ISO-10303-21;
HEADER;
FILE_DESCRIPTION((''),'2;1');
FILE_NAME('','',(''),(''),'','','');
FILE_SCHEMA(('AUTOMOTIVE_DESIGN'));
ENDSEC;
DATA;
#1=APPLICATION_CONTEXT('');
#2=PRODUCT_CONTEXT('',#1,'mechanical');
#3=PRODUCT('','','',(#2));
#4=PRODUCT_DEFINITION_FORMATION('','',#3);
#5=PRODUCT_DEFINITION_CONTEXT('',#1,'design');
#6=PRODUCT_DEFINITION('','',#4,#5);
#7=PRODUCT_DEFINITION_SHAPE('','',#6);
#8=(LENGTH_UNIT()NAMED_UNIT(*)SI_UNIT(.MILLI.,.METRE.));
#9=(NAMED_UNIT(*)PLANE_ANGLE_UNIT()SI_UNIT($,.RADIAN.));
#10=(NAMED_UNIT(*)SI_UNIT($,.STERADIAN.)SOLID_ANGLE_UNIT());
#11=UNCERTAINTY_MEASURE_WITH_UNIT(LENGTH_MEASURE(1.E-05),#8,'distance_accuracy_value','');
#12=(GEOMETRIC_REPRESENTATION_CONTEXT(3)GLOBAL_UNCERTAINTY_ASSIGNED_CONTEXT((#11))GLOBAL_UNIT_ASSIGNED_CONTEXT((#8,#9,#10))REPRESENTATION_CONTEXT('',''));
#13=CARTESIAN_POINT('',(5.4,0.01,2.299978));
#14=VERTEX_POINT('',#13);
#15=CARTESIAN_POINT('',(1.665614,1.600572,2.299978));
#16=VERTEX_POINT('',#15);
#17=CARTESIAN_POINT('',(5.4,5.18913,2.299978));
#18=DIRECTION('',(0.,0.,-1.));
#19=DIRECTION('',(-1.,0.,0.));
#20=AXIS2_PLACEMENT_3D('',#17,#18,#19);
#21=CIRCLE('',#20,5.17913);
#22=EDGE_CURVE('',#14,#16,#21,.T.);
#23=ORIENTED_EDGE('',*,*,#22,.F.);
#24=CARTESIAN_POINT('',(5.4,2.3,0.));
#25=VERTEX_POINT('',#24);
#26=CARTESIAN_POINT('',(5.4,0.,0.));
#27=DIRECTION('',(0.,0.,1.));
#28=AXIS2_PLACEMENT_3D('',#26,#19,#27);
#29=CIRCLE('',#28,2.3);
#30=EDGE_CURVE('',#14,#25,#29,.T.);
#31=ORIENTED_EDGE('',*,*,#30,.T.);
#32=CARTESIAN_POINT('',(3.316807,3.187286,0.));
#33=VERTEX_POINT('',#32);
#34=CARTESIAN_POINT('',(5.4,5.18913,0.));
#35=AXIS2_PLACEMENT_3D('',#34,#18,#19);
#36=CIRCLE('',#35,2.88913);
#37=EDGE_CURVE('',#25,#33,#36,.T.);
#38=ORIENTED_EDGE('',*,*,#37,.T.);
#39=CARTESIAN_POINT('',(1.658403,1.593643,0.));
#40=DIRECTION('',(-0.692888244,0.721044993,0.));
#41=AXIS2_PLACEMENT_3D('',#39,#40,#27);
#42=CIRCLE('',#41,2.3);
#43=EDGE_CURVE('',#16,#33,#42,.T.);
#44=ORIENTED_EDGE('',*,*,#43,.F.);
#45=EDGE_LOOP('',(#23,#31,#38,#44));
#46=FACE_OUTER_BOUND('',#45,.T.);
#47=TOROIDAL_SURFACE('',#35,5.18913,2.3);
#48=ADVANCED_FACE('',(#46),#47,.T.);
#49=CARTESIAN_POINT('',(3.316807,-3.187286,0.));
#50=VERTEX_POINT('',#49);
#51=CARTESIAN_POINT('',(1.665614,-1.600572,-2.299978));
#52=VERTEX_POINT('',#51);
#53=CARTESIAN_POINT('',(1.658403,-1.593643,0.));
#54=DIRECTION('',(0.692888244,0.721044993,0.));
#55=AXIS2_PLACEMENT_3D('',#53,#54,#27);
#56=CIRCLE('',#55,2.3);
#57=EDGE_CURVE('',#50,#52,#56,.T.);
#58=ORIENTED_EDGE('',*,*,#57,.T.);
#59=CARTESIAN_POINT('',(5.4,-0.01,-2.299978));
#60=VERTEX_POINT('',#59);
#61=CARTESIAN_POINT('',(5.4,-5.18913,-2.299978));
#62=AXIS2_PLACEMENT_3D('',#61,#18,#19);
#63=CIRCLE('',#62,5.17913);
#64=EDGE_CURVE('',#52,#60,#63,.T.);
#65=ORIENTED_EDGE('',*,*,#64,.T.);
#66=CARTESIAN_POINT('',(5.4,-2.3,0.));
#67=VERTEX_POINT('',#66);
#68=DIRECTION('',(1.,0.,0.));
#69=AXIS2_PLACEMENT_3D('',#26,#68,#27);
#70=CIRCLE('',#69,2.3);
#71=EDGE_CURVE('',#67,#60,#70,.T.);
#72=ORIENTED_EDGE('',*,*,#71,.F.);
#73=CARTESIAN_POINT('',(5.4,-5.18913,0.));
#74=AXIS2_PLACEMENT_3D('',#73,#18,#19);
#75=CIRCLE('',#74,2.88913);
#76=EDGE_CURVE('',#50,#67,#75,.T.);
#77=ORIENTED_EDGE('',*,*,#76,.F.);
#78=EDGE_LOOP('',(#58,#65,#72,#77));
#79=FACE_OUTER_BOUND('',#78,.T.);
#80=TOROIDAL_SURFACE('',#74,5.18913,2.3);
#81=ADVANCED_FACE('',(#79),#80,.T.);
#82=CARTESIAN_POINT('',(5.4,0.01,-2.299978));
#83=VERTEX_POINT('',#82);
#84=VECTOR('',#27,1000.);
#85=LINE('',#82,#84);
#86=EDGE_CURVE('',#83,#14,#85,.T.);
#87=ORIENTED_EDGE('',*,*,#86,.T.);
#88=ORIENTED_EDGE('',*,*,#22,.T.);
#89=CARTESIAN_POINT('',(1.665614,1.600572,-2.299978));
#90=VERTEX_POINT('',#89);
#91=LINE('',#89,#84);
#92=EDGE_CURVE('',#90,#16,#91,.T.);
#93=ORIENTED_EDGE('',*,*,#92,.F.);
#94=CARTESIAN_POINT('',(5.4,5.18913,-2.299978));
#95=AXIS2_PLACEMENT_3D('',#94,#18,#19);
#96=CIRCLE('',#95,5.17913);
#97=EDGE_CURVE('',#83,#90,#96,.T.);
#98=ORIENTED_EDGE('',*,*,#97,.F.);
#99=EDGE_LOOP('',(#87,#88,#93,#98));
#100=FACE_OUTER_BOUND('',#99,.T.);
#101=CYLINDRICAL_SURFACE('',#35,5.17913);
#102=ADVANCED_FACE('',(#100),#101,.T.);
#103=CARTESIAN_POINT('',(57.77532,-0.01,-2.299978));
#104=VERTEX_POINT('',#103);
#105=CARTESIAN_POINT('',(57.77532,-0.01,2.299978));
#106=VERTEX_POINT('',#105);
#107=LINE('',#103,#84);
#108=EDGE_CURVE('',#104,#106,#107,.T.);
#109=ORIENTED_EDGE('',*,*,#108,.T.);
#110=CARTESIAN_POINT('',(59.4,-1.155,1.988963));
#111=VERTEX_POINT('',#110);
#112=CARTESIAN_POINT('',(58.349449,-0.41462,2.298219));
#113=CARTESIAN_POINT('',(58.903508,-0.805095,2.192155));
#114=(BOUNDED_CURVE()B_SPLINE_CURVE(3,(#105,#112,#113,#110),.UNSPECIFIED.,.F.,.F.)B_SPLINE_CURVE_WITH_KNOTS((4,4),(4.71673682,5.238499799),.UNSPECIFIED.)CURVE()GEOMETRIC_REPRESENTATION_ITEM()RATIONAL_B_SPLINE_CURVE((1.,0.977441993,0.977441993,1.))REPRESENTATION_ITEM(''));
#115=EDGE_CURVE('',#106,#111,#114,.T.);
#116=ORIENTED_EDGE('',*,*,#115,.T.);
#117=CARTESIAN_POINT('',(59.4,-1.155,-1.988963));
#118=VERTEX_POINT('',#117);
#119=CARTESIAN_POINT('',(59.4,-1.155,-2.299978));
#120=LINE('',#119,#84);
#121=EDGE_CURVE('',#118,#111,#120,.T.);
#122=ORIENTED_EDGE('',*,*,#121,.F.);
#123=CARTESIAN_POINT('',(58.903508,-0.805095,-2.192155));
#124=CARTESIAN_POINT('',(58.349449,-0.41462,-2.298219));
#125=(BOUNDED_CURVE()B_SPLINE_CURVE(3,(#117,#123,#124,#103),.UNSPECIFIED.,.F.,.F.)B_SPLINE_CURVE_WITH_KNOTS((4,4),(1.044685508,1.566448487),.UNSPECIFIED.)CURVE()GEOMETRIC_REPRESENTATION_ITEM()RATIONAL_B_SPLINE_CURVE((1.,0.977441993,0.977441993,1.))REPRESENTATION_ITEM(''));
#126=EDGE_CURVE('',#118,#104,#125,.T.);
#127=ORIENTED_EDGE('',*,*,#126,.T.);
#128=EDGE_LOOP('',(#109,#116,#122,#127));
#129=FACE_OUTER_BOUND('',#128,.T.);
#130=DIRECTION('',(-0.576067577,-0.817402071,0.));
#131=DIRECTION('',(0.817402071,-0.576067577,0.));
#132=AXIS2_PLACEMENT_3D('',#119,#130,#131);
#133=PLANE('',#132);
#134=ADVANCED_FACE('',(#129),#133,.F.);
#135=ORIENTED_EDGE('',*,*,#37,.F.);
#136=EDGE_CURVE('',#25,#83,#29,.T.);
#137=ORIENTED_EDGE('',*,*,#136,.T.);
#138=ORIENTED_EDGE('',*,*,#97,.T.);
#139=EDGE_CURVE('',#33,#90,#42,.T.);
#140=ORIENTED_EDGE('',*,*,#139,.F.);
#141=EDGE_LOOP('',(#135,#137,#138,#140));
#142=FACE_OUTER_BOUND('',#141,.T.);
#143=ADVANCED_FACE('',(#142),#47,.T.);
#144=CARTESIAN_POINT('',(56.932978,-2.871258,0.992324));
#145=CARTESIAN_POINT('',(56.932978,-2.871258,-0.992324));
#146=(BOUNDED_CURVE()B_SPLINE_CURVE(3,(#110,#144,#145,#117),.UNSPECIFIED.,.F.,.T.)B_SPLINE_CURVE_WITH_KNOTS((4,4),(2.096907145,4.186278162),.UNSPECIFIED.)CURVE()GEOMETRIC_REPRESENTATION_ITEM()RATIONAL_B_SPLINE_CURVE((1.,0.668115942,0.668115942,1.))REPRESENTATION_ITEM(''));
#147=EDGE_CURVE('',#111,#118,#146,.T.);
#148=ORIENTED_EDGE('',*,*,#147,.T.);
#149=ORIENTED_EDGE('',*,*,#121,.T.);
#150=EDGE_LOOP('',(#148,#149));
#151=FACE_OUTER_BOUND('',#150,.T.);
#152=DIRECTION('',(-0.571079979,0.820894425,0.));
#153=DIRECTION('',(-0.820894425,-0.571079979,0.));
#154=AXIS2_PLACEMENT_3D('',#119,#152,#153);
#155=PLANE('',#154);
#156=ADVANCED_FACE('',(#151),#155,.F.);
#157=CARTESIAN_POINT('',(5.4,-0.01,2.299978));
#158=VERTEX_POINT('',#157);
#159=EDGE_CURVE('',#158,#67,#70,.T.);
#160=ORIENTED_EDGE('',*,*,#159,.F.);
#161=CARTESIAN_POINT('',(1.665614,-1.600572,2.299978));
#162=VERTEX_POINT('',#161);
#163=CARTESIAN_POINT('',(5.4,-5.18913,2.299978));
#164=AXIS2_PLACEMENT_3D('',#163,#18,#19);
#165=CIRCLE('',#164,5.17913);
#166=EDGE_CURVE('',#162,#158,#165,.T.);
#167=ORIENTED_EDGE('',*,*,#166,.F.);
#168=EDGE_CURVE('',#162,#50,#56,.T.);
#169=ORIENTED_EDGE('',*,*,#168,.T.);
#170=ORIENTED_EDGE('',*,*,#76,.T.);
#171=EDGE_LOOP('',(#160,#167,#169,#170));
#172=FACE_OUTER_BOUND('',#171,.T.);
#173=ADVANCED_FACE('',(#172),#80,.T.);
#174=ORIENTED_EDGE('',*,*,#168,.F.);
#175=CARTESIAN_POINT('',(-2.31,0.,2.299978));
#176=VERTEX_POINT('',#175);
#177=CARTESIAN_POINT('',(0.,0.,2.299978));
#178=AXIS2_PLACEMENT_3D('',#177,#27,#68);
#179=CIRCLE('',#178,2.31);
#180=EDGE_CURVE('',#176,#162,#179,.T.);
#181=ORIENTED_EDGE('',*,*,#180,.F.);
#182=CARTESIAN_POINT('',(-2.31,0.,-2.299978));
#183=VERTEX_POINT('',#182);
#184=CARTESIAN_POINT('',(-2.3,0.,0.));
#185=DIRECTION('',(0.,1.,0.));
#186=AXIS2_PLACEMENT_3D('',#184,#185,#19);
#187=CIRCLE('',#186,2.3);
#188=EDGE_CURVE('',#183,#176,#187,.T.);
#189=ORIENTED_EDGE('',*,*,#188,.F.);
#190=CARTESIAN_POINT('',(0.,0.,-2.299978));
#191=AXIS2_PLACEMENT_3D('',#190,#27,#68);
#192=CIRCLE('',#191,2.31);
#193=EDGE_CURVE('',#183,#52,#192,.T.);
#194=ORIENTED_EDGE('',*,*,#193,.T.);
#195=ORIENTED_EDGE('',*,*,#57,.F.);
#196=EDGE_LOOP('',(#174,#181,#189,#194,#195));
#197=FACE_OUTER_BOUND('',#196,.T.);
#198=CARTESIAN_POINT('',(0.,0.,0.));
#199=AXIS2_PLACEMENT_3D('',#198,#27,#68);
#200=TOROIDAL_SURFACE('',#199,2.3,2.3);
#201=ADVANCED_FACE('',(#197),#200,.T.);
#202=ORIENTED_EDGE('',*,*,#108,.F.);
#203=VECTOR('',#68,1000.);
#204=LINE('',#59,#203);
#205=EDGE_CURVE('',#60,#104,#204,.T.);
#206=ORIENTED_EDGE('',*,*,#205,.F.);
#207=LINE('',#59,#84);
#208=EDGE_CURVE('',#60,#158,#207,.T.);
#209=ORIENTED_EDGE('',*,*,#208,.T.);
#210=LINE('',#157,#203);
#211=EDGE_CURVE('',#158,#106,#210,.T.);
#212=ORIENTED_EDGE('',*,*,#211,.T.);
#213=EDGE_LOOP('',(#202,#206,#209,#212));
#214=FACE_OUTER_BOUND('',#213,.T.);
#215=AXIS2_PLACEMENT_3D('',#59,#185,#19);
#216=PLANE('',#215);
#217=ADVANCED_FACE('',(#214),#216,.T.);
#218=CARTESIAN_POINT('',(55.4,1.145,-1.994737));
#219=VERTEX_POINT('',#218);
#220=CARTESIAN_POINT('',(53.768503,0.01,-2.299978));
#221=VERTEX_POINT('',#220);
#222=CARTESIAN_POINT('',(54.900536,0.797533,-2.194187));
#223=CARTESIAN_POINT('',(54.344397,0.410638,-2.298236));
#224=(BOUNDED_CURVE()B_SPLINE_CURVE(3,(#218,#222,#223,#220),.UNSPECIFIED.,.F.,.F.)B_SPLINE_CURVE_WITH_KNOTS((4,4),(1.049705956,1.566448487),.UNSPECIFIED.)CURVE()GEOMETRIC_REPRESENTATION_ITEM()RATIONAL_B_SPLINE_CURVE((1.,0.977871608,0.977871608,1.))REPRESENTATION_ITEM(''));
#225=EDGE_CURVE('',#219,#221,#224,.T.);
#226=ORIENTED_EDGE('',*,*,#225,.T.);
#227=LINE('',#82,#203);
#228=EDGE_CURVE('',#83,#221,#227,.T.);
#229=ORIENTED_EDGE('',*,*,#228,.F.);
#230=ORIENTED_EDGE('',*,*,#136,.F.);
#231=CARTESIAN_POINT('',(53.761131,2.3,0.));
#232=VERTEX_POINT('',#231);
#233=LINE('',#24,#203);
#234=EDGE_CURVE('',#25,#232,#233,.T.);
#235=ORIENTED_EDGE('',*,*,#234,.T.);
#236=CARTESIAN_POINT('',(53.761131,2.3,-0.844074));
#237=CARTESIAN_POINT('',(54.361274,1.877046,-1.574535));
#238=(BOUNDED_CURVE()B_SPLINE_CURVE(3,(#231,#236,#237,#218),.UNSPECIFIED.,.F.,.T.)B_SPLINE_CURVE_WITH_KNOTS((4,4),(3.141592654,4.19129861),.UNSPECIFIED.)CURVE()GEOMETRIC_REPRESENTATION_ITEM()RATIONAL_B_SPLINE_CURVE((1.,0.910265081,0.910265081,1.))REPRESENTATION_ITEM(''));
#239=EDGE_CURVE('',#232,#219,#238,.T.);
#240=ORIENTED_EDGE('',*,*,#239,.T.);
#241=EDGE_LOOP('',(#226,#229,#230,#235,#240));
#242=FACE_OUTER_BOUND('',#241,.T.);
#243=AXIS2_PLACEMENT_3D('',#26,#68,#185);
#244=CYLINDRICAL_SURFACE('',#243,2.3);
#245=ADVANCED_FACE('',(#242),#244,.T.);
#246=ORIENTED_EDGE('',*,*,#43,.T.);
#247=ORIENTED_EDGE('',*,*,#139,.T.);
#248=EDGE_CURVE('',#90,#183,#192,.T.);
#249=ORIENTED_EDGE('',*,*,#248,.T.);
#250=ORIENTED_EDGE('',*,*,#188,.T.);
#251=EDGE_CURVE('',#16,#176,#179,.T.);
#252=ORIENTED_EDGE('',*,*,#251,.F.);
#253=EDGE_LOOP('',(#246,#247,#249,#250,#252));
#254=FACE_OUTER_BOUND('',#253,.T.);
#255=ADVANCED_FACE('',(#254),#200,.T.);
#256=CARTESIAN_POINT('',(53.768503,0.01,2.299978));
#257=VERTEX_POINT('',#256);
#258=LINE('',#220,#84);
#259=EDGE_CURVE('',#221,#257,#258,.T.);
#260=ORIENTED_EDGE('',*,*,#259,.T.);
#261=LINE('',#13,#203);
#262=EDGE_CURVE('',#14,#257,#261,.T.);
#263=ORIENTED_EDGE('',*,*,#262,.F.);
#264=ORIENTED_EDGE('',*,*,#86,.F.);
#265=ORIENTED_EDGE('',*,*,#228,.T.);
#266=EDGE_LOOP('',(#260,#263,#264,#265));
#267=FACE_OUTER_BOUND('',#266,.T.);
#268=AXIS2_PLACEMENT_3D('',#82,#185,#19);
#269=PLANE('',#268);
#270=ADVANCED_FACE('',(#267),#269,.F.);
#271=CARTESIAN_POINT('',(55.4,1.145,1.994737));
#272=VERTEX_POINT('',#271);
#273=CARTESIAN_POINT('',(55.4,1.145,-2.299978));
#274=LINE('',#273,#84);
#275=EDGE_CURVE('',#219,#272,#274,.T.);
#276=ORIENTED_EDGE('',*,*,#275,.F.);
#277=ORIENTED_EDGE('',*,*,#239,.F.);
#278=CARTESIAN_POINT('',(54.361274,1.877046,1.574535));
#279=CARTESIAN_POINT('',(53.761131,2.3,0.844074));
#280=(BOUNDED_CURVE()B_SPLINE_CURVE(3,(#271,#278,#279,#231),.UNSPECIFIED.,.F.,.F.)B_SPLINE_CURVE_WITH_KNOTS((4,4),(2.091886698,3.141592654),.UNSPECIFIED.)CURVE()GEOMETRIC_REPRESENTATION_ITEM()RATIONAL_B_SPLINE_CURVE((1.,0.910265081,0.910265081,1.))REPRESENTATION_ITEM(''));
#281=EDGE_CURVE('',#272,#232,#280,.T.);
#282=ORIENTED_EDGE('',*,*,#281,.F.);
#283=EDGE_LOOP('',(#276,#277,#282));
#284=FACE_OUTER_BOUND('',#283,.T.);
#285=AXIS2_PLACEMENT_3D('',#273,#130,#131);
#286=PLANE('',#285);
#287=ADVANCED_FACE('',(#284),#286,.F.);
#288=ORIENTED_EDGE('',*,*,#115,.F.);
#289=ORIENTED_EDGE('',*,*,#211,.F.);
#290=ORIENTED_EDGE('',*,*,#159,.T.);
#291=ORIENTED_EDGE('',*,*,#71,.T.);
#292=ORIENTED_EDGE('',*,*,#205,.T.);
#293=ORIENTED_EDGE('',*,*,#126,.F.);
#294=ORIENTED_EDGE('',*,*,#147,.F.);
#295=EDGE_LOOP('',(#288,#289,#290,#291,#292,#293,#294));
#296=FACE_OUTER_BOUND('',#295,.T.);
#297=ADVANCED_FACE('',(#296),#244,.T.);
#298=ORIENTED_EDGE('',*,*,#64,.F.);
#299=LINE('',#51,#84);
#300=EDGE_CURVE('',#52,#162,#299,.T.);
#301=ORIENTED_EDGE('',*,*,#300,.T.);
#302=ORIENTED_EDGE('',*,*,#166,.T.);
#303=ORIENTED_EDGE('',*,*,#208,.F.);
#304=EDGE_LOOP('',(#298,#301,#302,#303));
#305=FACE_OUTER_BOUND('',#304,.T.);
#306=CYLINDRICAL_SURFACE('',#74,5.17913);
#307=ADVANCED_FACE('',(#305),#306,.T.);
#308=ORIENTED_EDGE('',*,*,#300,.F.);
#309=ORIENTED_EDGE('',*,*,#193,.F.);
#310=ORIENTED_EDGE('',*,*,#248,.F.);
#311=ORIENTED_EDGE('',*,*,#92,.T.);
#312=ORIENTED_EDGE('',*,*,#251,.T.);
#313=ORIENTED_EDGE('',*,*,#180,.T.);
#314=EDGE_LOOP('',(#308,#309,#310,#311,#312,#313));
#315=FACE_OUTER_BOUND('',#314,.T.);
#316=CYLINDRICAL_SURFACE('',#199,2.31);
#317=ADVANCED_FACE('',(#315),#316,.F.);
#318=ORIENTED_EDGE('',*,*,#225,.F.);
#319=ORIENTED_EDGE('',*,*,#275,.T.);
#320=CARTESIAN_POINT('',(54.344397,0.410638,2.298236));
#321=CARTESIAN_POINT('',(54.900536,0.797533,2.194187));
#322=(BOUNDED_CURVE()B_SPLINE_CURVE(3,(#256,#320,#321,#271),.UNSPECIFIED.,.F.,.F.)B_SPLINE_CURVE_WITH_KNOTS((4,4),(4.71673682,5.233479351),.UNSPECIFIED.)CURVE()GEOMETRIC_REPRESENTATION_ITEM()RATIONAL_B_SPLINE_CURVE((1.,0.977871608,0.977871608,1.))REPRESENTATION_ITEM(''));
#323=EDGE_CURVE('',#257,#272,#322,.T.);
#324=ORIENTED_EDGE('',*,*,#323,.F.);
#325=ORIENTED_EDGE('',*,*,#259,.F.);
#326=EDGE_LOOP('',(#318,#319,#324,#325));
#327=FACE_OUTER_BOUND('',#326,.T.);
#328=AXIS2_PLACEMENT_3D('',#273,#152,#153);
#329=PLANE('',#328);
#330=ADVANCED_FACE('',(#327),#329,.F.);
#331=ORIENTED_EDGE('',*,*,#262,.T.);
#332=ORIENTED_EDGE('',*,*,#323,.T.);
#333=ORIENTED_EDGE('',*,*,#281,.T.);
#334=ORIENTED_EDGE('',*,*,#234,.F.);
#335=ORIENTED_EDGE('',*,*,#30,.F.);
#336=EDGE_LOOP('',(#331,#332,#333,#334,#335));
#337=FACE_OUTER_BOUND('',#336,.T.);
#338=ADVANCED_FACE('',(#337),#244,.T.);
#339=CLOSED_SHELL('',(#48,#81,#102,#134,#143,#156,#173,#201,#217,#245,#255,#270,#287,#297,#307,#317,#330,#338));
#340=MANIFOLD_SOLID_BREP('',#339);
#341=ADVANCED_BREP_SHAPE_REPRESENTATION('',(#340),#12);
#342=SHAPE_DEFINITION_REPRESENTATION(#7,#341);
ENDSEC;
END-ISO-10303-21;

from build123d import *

# Parameters (mm, degrees)
CUT_EXTRUDE1_DEPTH      = 60.622226572
CUT_EXTRUDE1_DEPTH_BACK = 60.622226572


with BuildPart() as part:
    # Sweep2: sweep along a path in Dimension sketch
    with BuildLine(Plane.XY) as sweep2_path:
        Line((55.4, 2.3), (5.4, 2.3))
        ThreePointArc((5.4, 2.3), (4.267859381, 2.531061156), (3.316806967, 3.187285922))
        ThreePointArc((3.316806967, 3.187285922), (-4.6, 0), (3.316806967, -3.187285922))
        ThreePointArc((3.316806967, -3.187285922), (4.267859381, -2.531061156), (5.4, -2.3))
        Line((5.4, -2.3), (59.4, -2.3))
    # Sketch2 → Sweep2 (sweep)
    with BuildSketch(Plane(origin=(55.4, 2.3, 0), x_dir=(0, 0, 1), z_dir=(-1, 0, 0))):
        with BuildLine():
            Line((-2.299978261, -2.29), (2.299978261, -2.29))
            ThreePointArc((2.299978261, -2.29), (0, 0), (-2.299978261, -2.29))
        make_face()
    sweep(path=sweep2_path.line)

    # Sketch3 → Cut-Extrude1 (cut, two sides: drawn at the far end of the back side and taken through both)
    with BuildSketch(Plane.XY.offset(-CUT_EXTRUDE1_DEPTH_BACK)):
        Polygon((55.4, 1.145), (53.76113083, 2.3), (59.41, 2.3), (59.41, -2.3), (57.754128755, -2.3), (59.4, -1.155), (57.76113083, 0), (53.754128755, 0), align=None)
    extrude(amount=CUT_EXTRUDE1_DEPTH + CUT_EXTRUDE1_DEPTH_BACK, mode=Mode.SUBTRACT)


solid = part.part
